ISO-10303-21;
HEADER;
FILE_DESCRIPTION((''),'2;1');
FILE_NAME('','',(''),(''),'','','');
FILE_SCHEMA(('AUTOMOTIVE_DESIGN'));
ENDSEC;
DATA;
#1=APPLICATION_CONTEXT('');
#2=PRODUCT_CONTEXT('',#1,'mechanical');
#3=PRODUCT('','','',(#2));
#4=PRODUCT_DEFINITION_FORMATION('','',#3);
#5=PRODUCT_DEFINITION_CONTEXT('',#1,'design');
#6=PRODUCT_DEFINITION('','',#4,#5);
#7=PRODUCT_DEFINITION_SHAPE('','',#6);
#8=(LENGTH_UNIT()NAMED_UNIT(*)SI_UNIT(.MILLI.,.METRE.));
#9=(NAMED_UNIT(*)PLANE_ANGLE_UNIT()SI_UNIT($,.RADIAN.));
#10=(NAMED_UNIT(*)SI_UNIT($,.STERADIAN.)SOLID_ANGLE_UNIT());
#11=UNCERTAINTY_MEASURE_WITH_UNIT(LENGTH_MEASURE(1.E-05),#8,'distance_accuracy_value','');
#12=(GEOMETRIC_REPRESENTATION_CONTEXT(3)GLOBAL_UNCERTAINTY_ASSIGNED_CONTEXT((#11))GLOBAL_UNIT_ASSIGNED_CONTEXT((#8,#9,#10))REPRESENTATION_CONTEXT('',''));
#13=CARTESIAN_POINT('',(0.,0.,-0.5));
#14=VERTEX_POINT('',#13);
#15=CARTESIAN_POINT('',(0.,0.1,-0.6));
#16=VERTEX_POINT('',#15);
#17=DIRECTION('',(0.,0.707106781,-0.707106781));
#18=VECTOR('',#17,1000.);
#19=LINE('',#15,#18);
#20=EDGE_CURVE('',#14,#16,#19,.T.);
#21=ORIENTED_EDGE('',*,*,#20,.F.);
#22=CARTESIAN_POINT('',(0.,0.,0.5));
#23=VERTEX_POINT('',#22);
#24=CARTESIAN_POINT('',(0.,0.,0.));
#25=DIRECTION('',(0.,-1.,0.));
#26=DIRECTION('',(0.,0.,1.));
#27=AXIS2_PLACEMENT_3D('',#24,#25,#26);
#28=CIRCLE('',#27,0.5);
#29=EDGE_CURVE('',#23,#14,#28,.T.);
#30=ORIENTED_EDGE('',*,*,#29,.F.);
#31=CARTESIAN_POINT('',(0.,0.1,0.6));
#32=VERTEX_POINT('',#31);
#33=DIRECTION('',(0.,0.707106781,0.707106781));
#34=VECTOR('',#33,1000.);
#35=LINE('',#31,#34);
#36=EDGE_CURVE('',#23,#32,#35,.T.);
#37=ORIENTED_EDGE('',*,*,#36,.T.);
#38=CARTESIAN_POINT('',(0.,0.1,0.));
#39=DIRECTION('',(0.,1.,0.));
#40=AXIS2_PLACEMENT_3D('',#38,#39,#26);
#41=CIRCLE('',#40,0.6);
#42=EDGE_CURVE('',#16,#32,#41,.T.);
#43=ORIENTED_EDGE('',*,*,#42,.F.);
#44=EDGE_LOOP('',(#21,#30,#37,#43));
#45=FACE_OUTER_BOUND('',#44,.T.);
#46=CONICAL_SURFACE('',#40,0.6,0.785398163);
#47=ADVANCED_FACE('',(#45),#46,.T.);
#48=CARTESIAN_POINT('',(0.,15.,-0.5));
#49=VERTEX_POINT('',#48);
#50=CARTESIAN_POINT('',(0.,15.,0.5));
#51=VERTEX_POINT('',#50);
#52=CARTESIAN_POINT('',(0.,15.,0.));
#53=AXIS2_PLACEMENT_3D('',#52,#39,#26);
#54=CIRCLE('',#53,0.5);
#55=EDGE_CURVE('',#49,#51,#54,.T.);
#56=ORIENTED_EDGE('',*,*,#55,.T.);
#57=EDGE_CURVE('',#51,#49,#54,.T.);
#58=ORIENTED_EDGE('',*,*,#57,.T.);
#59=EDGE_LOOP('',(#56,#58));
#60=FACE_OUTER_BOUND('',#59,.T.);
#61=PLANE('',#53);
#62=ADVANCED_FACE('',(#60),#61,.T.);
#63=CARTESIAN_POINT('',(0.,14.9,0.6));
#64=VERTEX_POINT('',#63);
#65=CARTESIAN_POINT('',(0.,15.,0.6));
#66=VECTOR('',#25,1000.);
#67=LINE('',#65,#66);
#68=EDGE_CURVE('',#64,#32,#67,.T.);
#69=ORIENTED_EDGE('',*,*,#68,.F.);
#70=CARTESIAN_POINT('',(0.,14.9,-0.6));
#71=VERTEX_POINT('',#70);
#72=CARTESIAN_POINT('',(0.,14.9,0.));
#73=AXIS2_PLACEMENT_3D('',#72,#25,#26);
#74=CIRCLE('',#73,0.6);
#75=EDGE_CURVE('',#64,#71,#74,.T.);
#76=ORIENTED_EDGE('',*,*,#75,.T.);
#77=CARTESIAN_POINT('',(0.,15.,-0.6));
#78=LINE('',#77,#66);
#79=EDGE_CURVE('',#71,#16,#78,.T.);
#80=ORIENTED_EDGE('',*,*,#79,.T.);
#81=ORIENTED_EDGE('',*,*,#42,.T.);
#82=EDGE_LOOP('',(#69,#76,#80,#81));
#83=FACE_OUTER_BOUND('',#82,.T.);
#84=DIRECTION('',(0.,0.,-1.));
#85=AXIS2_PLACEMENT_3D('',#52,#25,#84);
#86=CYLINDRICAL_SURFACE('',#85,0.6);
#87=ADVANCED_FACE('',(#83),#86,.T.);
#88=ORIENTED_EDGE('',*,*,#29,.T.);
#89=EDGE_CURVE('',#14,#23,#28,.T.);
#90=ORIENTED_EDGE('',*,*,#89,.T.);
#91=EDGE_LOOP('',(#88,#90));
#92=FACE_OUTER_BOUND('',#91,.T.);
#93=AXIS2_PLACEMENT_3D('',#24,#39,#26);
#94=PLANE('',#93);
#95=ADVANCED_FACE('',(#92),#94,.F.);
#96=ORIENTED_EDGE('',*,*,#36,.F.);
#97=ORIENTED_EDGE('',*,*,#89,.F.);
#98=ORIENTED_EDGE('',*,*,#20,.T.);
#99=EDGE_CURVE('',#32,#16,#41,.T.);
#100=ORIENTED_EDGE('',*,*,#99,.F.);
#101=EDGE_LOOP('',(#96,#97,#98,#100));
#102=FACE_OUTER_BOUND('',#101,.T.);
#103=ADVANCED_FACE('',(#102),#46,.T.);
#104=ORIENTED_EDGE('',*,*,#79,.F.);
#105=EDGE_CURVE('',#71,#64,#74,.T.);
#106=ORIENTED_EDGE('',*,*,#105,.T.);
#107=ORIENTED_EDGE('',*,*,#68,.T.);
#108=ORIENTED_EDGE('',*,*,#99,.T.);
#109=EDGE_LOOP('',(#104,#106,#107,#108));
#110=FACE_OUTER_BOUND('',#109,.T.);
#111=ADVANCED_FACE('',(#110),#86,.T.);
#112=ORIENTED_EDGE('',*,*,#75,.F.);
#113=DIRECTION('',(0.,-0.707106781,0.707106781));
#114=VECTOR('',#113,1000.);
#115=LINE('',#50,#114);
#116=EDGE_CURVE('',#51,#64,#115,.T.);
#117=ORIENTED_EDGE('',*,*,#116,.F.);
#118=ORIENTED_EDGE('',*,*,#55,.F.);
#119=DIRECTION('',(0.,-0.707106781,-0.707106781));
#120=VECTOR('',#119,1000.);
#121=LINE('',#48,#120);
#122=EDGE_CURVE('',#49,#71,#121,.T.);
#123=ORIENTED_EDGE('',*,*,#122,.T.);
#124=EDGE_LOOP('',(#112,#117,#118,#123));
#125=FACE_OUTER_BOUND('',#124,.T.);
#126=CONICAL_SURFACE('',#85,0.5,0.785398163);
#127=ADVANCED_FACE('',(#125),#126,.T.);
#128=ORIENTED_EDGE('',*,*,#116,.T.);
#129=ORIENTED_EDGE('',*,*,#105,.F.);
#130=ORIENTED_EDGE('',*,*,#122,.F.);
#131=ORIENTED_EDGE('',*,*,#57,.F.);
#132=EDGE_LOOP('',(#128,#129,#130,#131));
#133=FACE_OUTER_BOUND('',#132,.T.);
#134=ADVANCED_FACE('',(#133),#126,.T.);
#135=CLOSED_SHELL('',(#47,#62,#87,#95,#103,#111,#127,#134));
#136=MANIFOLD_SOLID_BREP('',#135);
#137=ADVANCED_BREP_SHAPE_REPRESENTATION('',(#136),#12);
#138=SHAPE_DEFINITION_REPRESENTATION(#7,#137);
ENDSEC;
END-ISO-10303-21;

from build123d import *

# Parameters (mm, degrees)
SKETCH1_R           = 0.6
BOSS_EXTRUDE1_DEPTH = 15
CHAMFER1_SIZE       = 0.1


with BuildPart() as part:
    # Sketch1 → Boss-Extrude1 (new body)
    with BuildSketch(Plane(origin=(0, 0, 0), x_dir=(1, 0, 0), z_dir=(0, 1, 0))):
        with Locations(Location((0, 0, 0), (0, 0, 270))):
            Circle(SKETCH1_R)
    extrude(amount=BOSS_EXTRUDE1_DEPTH)

    # Chamfer1
    chamfer1_edges = [part.edges().sort_by_distance(p)[0] for p in [
        (0, 0, -0.6),
        (0, 15, -0.6),
    ]]
    chamfer(chamfer1_edges, length=CHAMFER1_SIZE)


solid = part.part
